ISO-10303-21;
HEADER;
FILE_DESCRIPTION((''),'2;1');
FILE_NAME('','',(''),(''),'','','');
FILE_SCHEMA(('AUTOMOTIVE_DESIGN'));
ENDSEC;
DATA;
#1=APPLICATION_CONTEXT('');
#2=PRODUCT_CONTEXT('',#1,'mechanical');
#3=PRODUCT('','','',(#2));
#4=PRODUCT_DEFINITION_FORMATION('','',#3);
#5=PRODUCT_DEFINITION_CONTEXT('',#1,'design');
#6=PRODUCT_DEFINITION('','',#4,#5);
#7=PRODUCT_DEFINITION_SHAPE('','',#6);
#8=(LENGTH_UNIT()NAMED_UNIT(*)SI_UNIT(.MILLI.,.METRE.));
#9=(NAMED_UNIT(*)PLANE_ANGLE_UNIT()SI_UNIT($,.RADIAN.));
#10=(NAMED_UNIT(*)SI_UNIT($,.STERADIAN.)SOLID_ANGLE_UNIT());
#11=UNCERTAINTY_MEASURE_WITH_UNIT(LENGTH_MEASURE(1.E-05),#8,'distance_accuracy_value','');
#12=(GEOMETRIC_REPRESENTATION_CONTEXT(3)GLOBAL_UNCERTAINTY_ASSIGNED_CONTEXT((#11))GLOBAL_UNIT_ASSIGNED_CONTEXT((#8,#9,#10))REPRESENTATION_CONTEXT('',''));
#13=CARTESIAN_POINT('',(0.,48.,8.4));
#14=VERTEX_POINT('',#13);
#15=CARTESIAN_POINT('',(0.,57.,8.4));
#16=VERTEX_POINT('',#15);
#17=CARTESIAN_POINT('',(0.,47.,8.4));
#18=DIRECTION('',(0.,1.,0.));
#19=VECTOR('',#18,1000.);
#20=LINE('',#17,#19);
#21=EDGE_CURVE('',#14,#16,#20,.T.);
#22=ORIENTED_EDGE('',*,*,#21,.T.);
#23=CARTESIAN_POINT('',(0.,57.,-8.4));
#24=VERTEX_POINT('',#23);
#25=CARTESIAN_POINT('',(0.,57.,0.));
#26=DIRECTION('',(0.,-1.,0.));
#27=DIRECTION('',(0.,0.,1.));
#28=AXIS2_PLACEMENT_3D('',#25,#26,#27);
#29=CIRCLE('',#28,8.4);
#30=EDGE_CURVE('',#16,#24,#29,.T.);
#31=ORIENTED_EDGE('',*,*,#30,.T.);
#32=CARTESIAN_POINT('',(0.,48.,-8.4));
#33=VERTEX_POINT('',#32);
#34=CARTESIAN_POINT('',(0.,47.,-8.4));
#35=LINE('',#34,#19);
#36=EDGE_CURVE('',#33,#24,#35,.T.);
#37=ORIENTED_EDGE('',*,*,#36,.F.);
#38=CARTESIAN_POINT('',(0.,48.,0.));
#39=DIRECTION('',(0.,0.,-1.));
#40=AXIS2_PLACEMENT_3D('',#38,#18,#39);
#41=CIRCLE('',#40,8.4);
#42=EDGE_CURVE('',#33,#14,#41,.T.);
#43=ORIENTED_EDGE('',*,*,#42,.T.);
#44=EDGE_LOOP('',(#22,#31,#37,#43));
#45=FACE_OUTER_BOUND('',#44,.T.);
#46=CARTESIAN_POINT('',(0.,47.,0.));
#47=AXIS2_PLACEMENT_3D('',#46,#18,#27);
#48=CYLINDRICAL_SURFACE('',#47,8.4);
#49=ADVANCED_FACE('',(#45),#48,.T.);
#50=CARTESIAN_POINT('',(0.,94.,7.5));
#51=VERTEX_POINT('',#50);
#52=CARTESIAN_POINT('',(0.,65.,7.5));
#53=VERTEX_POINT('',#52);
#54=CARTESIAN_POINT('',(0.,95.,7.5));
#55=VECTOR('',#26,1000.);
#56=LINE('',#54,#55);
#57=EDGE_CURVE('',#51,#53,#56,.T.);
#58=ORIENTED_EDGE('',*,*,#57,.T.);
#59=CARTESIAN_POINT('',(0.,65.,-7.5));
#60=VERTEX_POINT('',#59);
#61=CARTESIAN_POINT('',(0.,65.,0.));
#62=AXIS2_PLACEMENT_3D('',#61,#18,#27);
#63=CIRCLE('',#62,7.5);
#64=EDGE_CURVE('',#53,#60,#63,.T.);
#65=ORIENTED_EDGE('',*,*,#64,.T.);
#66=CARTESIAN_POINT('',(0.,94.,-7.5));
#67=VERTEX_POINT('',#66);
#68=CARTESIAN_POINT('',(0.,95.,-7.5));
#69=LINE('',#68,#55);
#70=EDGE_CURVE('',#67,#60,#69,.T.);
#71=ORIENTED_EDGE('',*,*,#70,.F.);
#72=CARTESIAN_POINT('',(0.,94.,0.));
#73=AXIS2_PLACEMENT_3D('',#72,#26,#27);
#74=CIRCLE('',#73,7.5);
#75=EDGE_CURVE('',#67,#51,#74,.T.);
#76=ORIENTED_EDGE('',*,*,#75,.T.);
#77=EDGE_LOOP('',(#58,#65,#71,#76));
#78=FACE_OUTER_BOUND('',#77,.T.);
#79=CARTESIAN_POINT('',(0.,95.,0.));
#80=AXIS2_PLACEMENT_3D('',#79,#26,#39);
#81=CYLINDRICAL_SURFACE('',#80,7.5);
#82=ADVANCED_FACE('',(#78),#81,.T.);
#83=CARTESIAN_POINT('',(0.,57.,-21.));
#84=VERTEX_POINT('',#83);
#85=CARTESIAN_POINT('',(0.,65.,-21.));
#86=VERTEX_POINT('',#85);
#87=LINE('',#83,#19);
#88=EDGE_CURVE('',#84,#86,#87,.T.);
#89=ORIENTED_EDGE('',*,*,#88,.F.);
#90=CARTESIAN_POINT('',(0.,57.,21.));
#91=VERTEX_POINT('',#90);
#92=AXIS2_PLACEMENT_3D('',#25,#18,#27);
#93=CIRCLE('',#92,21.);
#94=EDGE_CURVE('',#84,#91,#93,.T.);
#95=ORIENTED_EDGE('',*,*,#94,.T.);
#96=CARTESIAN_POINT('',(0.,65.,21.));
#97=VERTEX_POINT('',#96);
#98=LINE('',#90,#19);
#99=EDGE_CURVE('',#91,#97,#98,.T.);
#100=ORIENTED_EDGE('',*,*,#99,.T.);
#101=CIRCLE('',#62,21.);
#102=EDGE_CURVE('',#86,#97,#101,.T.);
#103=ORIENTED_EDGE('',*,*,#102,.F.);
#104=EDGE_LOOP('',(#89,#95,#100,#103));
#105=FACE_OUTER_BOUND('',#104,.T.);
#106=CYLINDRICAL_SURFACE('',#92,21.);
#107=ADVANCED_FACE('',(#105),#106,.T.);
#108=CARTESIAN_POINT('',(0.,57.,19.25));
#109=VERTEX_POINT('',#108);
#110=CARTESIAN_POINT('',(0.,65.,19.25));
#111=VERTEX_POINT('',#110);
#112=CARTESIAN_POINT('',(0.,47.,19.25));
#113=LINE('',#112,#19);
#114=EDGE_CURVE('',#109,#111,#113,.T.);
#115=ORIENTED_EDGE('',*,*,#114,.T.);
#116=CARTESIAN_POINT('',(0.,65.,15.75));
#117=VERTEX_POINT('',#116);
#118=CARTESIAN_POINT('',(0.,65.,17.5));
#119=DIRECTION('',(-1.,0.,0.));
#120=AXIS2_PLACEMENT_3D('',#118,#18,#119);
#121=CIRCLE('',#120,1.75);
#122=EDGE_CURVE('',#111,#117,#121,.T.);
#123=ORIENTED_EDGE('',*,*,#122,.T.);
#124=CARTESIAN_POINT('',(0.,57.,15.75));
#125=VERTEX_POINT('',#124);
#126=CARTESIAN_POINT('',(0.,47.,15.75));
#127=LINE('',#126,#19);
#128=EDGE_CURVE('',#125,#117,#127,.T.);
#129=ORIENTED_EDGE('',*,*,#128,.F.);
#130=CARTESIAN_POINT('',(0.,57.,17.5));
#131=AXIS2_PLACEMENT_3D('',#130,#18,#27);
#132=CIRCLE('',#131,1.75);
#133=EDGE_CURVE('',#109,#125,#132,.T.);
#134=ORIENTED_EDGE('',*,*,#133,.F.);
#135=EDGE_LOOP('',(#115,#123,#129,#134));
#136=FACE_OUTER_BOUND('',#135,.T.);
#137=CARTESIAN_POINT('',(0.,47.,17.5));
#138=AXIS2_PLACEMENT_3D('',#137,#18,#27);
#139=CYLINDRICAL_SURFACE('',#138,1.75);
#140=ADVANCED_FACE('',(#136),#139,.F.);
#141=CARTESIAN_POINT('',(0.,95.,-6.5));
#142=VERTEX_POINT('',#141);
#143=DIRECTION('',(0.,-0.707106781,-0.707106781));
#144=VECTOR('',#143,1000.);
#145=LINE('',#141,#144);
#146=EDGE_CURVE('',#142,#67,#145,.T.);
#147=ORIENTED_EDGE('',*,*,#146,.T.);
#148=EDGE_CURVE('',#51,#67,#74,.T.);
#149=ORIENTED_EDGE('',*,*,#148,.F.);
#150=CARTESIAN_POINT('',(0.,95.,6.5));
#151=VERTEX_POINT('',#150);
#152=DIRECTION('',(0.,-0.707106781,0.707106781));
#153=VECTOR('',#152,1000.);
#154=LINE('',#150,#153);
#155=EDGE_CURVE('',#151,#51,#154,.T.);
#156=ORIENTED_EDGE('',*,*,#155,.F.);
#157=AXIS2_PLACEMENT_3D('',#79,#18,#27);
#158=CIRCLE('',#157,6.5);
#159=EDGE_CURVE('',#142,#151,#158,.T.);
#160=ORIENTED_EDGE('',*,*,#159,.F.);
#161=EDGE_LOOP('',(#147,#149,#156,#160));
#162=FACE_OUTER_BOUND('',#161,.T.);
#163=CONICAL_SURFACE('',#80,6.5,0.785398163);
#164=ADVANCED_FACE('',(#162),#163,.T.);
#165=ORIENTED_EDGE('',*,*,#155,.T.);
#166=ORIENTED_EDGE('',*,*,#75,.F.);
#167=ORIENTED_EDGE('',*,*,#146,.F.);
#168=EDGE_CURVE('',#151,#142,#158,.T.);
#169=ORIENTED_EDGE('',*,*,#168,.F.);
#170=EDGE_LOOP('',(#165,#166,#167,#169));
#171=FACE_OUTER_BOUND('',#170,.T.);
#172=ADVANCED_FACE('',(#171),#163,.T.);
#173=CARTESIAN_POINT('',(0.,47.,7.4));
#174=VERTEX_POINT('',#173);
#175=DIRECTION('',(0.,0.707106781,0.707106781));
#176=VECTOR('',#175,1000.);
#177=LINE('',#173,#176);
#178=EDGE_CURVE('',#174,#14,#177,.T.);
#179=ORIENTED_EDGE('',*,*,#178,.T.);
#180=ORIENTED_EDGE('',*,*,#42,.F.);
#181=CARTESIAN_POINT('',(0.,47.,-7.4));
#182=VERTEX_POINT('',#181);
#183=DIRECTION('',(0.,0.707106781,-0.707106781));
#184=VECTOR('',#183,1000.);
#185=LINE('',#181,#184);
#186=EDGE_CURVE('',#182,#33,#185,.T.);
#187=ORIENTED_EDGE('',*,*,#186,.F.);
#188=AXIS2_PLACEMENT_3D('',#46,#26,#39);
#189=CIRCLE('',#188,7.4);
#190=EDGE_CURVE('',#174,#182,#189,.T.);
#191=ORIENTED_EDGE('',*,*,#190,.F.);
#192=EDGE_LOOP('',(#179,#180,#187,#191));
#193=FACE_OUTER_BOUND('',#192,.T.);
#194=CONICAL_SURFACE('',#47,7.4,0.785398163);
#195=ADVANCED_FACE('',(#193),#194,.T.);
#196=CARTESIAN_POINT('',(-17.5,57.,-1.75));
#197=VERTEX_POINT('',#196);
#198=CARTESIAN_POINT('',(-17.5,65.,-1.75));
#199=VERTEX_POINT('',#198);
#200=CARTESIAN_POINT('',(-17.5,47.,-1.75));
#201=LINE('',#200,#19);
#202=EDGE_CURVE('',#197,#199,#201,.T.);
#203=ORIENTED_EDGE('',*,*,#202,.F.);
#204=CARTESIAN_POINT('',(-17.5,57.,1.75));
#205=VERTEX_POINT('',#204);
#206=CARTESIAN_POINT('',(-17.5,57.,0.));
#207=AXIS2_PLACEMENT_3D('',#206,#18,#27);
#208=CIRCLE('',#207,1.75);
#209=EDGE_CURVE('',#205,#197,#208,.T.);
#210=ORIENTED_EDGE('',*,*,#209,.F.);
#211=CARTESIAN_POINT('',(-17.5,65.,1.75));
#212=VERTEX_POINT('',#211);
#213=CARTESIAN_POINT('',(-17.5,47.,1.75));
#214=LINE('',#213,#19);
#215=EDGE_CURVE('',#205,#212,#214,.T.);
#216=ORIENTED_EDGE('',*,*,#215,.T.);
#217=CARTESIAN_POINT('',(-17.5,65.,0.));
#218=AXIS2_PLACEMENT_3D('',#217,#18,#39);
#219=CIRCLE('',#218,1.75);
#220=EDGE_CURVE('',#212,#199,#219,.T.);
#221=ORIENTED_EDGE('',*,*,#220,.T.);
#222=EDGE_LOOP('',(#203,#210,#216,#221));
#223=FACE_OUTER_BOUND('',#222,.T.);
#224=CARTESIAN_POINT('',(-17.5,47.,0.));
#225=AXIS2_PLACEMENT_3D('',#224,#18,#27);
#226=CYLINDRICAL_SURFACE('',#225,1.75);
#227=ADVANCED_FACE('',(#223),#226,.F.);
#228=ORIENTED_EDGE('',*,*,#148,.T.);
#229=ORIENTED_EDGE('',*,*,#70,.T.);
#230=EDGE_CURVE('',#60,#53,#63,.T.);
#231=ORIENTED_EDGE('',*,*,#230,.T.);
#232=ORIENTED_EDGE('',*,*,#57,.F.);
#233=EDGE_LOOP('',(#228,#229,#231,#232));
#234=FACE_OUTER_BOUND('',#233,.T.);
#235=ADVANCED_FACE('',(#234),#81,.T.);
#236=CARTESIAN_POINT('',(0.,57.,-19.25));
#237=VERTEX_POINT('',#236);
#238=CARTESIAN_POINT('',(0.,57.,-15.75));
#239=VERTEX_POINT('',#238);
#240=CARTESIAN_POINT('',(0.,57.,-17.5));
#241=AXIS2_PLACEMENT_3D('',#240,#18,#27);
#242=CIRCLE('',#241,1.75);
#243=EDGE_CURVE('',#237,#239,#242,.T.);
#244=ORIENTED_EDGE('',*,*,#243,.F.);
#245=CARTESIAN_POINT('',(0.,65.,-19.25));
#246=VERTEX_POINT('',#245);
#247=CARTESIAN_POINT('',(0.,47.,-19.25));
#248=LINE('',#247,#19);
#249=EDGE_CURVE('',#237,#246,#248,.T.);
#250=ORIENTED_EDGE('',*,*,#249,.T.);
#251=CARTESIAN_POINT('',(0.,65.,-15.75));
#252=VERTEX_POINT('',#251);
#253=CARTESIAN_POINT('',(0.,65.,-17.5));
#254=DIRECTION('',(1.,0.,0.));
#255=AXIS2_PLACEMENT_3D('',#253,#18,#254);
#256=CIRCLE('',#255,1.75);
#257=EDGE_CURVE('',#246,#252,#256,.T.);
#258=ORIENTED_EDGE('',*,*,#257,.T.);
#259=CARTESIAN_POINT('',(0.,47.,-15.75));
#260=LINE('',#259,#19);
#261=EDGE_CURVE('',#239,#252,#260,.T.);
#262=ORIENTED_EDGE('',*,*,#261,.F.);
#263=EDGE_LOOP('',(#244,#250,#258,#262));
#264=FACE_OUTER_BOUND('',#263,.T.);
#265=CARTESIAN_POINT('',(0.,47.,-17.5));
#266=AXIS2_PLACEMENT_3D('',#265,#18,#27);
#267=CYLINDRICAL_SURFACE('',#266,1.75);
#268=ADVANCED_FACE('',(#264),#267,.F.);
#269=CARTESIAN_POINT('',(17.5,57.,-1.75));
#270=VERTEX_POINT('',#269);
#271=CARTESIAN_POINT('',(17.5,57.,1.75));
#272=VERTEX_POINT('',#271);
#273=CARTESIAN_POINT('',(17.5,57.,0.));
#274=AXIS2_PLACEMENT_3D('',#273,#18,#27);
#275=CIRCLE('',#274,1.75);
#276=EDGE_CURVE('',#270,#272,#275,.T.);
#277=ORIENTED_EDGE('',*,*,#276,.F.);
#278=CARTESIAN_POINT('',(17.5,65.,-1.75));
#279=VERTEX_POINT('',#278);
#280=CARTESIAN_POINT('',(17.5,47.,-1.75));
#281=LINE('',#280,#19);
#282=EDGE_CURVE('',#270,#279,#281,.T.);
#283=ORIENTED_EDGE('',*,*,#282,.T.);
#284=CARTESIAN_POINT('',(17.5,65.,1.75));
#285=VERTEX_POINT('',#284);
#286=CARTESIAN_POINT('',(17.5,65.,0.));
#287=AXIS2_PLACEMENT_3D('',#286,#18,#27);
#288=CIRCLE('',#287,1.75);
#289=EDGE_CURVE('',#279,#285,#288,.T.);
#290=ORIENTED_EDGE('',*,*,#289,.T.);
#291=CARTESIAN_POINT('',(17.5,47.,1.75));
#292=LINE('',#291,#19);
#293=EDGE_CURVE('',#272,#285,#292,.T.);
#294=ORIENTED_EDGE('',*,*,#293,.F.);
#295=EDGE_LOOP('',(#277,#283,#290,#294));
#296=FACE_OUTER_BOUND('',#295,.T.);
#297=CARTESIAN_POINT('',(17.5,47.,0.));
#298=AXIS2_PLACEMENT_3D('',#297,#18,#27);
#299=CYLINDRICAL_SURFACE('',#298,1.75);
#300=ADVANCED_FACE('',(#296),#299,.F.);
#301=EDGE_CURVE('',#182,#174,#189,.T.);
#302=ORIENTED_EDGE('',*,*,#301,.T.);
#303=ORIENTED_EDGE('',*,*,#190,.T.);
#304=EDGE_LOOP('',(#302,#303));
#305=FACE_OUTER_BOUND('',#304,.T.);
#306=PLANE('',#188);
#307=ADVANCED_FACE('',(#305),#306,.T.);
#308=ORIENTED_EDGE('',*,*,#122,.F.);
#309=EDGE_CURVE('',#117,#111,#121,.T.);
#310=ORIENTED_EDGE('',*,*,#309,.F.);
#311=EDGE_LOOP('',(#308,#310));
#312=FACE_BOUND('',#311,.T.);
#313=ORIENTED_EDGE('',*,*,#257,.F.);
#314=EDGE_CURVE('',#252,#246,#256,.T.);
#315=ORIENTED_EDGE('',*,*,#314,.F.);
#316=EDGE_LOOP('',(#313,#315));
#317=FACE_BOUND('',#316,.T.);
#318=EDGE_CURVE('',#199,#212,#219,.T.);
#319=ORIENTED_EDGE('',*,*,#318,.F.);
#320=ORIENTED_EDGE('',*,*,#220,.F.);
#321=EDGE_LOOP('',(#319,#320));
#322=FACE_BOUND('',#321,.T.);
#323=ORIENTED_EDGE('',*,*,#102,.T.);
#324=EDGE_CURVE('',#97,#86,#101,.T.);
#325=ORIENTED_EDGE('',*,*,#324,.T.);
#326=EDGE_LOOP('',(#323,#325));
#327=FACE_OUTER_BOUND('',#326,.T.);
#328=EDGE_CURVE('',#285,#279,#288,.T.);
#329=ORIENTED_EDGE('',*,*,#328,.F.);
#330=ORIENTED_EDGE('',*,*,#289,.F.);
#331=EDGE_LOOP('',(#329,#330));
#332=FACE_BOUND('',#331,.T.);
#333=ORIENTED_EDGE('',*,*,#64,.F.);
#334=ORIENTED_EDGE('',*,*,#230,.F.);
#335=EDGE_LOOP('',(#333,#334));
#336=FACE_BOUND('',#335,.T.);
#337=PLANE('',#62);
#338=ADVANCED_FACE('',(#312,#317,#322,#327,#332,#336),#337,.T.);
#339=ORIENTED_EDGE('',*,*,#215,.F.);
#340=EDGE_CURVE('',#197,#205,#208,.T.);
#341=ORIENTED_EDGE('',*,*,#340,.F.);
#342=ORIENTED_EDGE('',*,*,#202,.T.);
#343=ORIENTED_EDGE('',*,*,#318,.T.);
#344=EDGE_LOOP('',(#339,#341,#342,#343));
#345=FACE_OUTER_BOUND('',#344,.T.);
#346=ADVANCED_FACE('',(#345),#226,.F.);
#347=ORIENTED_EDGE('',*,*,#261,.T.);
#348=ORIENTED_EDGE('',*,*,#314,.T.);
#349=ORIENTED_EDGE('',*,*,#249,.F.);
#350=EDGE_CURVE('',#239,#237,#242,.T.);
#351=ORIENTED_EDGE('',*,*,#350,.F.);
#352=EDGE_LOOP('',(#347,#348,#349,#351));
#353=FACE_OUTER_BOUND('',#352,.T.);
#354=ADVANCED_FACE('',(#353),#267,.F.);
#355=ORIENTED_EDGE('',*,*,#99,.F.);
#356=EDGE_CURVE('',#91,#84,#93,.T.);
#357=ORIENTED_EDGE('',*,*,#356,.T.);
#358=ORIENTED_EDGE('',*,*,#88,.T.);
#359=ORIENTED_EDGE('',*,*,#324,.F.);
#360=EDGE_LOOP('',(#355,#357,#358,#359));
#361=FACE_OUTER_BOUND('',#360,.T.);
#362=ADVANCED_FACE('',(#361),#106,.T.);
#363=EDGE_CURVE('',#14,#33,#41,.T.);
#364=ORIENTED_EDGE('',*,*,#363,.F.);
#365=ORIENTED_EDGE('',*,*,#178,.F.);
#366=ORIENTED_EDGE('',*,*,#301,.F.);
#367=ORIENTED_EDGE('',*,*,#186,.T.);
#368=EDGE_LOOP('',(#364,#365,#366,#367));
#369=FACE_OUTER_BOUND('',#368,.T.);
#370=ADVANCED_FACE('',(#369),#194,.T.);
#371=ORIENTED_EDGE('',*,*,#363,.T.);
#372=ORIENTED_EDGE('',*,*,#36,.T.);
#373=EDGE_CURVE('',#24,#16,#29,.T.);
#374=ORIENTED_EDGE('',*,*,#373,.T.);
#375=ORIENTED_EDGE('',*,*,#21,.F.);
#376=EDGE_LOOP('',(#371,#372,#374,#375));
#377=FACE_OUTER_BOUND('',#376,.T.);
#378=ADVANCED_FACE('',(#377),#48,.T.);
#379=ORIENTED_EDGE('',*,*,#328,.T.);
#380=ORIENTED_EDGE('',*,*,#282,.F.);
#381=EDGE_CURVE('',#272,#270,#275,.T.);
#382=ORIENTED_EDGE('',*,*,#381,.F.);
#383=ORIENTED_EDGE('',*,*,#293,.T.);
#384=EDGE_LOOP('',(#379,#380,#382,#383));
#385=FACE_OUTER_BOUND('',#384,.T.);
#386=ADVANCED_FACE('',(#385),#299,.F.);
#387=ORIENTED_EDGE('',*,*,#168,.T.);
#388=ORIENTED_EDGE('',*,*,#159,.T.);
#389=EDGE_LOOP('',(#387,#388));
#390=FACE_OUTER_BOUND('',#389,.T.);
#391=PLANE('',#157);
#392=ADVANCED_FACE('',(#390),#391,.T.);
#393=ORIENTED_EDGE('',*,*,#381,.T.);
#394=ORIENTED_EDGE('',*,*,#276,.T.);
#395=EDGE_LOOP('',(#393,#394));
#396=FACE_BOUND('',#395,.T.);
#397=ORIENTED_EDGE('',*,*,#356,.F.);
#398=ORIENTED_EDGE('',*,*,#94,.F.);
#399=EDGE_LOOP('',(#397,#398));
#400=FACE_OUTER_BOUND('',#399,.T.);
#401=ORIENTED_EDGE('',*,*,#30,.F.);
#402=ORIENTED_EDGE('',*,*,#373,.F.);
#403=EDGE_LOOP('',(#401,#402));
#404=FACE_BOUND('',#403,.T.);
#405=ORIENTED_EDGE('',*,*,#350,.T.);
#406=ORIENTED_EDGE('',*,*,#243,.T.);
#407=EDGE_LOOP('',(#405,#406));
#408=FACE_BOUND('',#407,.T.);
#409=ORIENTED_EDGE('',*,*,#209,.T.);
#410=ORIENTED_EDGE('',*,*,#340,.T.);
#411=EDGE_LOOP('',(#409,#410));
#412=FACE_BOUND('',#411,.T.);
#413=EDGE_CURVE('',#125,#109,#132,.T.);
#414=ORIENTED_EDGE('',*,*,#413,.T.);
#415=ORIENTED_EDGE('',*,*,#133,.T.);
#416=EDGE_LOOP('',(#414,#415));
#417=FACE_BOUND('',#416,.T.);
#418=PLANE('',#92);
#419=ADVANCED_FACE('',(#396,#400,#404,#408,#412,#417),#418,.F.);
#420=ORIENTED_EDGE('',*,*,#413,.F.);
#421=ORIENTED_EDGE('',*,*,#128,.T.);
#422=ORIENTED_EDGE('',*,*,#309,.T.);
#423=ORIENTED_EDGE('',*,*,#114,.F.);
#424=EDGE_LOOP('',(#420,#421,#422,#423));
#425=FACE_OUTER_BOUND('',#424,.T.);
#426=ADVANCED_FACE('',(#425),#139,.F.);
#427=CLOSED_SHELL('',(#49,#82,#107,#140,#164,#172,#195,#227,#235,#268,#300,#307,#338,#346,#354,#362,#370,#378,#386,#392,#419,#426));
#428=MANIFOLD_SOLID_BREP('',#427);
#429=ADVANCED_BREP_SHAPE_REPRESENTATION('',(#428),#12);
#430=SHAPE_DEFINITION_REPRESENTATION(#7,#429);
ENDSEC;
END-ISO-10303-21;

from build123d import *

# Parameters (mm, degrees)
SKETCH1_R           = 15
BOSS_EXTRUDE1_DEPTH = 65
SKETCH2_R           = 14
BOSS_EXTRUDE2_DEPTH = 260
SKETCH3_W           = 22.007775422
SKETCH3_H           = 2
CUT_EXTRUDE1_DEPTH  = 22
CIRPATTERN1_COUNT   = 4
SKETCH4_R           = 10.5
BOSS_EXTRUDE3_DEPTH = 30
SKETCH5_R           = 10.3
BOSS_EXTRUDE4_DEPTH = 10
SKETCH6_R           = 10.5
BOSS_EXTRUDE5_DEPTH = 16
CHAMFER1_SIZE       = 8
CHAMFER1_SIZE2      = 1
SKETCH8_R           = 7.5
BOSS_EXTRUDE6_DEPTH = 30
BOSS_EXTRUDE7_START = -8
SKETCH11_R          = 21
SKETCH11_R_2        = 15
BOSS_EXTRUDE7_DEPTH = 8
SKETCH13_R          = 19
CUT_EXTRUDE4_DEPTH  = 373
SKETCH14_R          = 8.4
BOSS_EXTRUDE8_DEPTH = 10
CHAMFER3_SIZE       = 1
SKETCH16_R          = 1.75
CUT_EXTRUDE5_DEPTH  = 43.213741838
CIRPATTERN3_COUNT   = 4


with BuildPart() as part:
    # Sketch1 → Boss-Extrude1 (new body)
    with BuildSketch(Plane(origin=(0, 0, 0), x_dir=(1, 0, 0), z_dir=(0, 1, 0))):
        with Locations(Location((0, 0, 0), (0, 0, 270))):
            Circle(SKETCH1_R)
    extrude(amount=BOSS_EXTRUDE1_DEPTH)

    # Sketch2 → Boss-Extrude2 (add)
    with BuildSketch(Plane.XZ):
        with Locations(Location((0, 0, 0), (0, 0, 90))):
            Circle(SKETCH2_R)
    extrude(amount=BOSS_EXTRUDE2_DEPTH)

    # Sketch3 → Cut-Extrude1 (cut)
    with BuildSketch(Plane.XZ.offset(260)):
        with Locations((0, -14)):
            Rectangle(SKETCH3_W, SKETCH3_H)
        with Locations((0, 14)):
            Rectangle(SKETCH3_W, SKETCH3_H)
    cut_extrude1 = extrude(amount=-CUT_EXTRUDE1_DEPTH, mode=Mode.SUBTRACT)

    # CirPattern1: Cut-Extrude1 ×4 about axis
    cirpattern1_axis = Axis((0, -260, 0), (0, 1, 0))
    for i in range(1, CIRPATTERN1_COUNT):
        add(cut_extrude1.rotate(cirpattern1_axis, i * 360 / CIRPATTERN1_COUNT), mode=Mode.SUBTRACT)

    # Sketch4 → Boss-Extrude3 (add)
    with BuildSketch(Plane.XZ.offset(260)):
        with Locations(Location((0, 0, 0), (0, 0, 270))):
            Circle(SKETCH4_R)
    extrude(amount=BOSS_EXTRUDE3_DEPTH)

    # Sketch5 → Boss-Extrude4 (add)
    with BuildSketch(Plane.XZ.offset(290)):
        with Locations(Location((0, 0, 0), (0, 0, 270))):
            Circle(SKETCH5_R)
    extrude(amount=BOSS_EXTRUDE4_DEPTH)

    # Sketch6 → Boss-Extrude5 (add)
    with BuildSketch(Plane.XZ.offset(300)):
        with Locations(Location((0, 0, 0), (0, 0, 270))):
            Circle(SKETCH6_R)
    extrude(amount=BOSS_EXTRUDE5_DEPTH)

    # Chamfer1
    chamfer1_edges = [part.edges().sort_by_distance(p)[0] for p in [
        (0, -316, 10.5),
    ]]
    chamfer1_side = [part.faces().sort_by_distance(p)[0] for p in [
        (0, -308, 10.5),
    ]]
    chamfer(chamfer1_edges, length=CHAMFER1_SIZE, length2=CHAMFER1_SIZE2, reference=chamfer1_side[0])

    # Sketch8 → Boss-Extrude6 (add)
    with BuildSketch(Plane(origin=(0, 65, 0), x_dir=(1, 0, 0), z_dir=(0, 1, 0))):
        with Locations(Location((0, 0, 0), (0, 0, 270))):
            Circle(SKETCH8_R)
    extrude(amount=BOSS_EXTRUDE6_DEPTH)

    # Sketch11 → Boss-Extrude7 (add)
    with BuildSketch(Plane(origin=(0, 65, 0), x_dir=(1, 0, 0), z_dir=(0, 1, 0)).offset(BOSS_EXTRUDE7_START)):
        with Locations(Location((0, 0, 0), (0, 0, 270))):
            Circle(SKETCH11_R)
        with Locations(Location((0, 0, 0), (0, 0, 270))):
            Circle(SKETCH11_R_2, mode=Mode.SUBTRACT)
    extrude(amount=BOSS_EXTRUDE7_DEPTH)

    # Sketch13 → Cut-Extrude4 (cut)
    with BuildSketch(Plane.XZ.offset(316)):
        Circle(SKETCH13_R)
    extrude(amount=-CUT_EXTRUDE4_DEPTH, mode=Mode.SUBTRACT)

    # Sketch14 → Boss-Extrude8 (add)
    with BuildSketch(Plane.XZ.offset(-57)):
        with Locations(Location((0, 0, 0), (0, 0, 90))):
            Circle(SKETCH14_R)
    extrude(amount=BOSS_EXTRUDE8_DEPTH)

    # Chamfer3
    chamfer3_edges = [part.edges().sort_by_distance(p)[0] for p in [
        (0, 95, -7.5),
        (0, 47, -8.4),
    ]]
    chamfer(chamfer3_edges, length=CHAMFER3_SIZE)

    # Sketch16 → Cut-Extrude5 (cut, through all)
    with BuildSketch(Plane(origin=(0, 65, 0), x_dir=(1, 0, 0), z_dir=(0, 1, 0))):
        with Locations(Location((17.5, 0, 0), (0, 0, 270))):
            Circle(SKETCH16_R)
    cut_extrude5 = extrude(amount=-CUT_EXTRUDE5_DEPTH, mode=Mode.SUBTRACT)

    # CirPattern3: Cut-Extrude5 ×4 about axis
    cirpattern3_axis = Axis((0, 0, 0), (0, 1, 0))
    for i in range(1, CIRPATTERN3_COUNT):
        add(cut_extrude5.rotate(cirpattern3_axis, i * 360 / CIRPATTERN3_COUNT), mode=Mode.SUBTRACT)


solid = part.part
